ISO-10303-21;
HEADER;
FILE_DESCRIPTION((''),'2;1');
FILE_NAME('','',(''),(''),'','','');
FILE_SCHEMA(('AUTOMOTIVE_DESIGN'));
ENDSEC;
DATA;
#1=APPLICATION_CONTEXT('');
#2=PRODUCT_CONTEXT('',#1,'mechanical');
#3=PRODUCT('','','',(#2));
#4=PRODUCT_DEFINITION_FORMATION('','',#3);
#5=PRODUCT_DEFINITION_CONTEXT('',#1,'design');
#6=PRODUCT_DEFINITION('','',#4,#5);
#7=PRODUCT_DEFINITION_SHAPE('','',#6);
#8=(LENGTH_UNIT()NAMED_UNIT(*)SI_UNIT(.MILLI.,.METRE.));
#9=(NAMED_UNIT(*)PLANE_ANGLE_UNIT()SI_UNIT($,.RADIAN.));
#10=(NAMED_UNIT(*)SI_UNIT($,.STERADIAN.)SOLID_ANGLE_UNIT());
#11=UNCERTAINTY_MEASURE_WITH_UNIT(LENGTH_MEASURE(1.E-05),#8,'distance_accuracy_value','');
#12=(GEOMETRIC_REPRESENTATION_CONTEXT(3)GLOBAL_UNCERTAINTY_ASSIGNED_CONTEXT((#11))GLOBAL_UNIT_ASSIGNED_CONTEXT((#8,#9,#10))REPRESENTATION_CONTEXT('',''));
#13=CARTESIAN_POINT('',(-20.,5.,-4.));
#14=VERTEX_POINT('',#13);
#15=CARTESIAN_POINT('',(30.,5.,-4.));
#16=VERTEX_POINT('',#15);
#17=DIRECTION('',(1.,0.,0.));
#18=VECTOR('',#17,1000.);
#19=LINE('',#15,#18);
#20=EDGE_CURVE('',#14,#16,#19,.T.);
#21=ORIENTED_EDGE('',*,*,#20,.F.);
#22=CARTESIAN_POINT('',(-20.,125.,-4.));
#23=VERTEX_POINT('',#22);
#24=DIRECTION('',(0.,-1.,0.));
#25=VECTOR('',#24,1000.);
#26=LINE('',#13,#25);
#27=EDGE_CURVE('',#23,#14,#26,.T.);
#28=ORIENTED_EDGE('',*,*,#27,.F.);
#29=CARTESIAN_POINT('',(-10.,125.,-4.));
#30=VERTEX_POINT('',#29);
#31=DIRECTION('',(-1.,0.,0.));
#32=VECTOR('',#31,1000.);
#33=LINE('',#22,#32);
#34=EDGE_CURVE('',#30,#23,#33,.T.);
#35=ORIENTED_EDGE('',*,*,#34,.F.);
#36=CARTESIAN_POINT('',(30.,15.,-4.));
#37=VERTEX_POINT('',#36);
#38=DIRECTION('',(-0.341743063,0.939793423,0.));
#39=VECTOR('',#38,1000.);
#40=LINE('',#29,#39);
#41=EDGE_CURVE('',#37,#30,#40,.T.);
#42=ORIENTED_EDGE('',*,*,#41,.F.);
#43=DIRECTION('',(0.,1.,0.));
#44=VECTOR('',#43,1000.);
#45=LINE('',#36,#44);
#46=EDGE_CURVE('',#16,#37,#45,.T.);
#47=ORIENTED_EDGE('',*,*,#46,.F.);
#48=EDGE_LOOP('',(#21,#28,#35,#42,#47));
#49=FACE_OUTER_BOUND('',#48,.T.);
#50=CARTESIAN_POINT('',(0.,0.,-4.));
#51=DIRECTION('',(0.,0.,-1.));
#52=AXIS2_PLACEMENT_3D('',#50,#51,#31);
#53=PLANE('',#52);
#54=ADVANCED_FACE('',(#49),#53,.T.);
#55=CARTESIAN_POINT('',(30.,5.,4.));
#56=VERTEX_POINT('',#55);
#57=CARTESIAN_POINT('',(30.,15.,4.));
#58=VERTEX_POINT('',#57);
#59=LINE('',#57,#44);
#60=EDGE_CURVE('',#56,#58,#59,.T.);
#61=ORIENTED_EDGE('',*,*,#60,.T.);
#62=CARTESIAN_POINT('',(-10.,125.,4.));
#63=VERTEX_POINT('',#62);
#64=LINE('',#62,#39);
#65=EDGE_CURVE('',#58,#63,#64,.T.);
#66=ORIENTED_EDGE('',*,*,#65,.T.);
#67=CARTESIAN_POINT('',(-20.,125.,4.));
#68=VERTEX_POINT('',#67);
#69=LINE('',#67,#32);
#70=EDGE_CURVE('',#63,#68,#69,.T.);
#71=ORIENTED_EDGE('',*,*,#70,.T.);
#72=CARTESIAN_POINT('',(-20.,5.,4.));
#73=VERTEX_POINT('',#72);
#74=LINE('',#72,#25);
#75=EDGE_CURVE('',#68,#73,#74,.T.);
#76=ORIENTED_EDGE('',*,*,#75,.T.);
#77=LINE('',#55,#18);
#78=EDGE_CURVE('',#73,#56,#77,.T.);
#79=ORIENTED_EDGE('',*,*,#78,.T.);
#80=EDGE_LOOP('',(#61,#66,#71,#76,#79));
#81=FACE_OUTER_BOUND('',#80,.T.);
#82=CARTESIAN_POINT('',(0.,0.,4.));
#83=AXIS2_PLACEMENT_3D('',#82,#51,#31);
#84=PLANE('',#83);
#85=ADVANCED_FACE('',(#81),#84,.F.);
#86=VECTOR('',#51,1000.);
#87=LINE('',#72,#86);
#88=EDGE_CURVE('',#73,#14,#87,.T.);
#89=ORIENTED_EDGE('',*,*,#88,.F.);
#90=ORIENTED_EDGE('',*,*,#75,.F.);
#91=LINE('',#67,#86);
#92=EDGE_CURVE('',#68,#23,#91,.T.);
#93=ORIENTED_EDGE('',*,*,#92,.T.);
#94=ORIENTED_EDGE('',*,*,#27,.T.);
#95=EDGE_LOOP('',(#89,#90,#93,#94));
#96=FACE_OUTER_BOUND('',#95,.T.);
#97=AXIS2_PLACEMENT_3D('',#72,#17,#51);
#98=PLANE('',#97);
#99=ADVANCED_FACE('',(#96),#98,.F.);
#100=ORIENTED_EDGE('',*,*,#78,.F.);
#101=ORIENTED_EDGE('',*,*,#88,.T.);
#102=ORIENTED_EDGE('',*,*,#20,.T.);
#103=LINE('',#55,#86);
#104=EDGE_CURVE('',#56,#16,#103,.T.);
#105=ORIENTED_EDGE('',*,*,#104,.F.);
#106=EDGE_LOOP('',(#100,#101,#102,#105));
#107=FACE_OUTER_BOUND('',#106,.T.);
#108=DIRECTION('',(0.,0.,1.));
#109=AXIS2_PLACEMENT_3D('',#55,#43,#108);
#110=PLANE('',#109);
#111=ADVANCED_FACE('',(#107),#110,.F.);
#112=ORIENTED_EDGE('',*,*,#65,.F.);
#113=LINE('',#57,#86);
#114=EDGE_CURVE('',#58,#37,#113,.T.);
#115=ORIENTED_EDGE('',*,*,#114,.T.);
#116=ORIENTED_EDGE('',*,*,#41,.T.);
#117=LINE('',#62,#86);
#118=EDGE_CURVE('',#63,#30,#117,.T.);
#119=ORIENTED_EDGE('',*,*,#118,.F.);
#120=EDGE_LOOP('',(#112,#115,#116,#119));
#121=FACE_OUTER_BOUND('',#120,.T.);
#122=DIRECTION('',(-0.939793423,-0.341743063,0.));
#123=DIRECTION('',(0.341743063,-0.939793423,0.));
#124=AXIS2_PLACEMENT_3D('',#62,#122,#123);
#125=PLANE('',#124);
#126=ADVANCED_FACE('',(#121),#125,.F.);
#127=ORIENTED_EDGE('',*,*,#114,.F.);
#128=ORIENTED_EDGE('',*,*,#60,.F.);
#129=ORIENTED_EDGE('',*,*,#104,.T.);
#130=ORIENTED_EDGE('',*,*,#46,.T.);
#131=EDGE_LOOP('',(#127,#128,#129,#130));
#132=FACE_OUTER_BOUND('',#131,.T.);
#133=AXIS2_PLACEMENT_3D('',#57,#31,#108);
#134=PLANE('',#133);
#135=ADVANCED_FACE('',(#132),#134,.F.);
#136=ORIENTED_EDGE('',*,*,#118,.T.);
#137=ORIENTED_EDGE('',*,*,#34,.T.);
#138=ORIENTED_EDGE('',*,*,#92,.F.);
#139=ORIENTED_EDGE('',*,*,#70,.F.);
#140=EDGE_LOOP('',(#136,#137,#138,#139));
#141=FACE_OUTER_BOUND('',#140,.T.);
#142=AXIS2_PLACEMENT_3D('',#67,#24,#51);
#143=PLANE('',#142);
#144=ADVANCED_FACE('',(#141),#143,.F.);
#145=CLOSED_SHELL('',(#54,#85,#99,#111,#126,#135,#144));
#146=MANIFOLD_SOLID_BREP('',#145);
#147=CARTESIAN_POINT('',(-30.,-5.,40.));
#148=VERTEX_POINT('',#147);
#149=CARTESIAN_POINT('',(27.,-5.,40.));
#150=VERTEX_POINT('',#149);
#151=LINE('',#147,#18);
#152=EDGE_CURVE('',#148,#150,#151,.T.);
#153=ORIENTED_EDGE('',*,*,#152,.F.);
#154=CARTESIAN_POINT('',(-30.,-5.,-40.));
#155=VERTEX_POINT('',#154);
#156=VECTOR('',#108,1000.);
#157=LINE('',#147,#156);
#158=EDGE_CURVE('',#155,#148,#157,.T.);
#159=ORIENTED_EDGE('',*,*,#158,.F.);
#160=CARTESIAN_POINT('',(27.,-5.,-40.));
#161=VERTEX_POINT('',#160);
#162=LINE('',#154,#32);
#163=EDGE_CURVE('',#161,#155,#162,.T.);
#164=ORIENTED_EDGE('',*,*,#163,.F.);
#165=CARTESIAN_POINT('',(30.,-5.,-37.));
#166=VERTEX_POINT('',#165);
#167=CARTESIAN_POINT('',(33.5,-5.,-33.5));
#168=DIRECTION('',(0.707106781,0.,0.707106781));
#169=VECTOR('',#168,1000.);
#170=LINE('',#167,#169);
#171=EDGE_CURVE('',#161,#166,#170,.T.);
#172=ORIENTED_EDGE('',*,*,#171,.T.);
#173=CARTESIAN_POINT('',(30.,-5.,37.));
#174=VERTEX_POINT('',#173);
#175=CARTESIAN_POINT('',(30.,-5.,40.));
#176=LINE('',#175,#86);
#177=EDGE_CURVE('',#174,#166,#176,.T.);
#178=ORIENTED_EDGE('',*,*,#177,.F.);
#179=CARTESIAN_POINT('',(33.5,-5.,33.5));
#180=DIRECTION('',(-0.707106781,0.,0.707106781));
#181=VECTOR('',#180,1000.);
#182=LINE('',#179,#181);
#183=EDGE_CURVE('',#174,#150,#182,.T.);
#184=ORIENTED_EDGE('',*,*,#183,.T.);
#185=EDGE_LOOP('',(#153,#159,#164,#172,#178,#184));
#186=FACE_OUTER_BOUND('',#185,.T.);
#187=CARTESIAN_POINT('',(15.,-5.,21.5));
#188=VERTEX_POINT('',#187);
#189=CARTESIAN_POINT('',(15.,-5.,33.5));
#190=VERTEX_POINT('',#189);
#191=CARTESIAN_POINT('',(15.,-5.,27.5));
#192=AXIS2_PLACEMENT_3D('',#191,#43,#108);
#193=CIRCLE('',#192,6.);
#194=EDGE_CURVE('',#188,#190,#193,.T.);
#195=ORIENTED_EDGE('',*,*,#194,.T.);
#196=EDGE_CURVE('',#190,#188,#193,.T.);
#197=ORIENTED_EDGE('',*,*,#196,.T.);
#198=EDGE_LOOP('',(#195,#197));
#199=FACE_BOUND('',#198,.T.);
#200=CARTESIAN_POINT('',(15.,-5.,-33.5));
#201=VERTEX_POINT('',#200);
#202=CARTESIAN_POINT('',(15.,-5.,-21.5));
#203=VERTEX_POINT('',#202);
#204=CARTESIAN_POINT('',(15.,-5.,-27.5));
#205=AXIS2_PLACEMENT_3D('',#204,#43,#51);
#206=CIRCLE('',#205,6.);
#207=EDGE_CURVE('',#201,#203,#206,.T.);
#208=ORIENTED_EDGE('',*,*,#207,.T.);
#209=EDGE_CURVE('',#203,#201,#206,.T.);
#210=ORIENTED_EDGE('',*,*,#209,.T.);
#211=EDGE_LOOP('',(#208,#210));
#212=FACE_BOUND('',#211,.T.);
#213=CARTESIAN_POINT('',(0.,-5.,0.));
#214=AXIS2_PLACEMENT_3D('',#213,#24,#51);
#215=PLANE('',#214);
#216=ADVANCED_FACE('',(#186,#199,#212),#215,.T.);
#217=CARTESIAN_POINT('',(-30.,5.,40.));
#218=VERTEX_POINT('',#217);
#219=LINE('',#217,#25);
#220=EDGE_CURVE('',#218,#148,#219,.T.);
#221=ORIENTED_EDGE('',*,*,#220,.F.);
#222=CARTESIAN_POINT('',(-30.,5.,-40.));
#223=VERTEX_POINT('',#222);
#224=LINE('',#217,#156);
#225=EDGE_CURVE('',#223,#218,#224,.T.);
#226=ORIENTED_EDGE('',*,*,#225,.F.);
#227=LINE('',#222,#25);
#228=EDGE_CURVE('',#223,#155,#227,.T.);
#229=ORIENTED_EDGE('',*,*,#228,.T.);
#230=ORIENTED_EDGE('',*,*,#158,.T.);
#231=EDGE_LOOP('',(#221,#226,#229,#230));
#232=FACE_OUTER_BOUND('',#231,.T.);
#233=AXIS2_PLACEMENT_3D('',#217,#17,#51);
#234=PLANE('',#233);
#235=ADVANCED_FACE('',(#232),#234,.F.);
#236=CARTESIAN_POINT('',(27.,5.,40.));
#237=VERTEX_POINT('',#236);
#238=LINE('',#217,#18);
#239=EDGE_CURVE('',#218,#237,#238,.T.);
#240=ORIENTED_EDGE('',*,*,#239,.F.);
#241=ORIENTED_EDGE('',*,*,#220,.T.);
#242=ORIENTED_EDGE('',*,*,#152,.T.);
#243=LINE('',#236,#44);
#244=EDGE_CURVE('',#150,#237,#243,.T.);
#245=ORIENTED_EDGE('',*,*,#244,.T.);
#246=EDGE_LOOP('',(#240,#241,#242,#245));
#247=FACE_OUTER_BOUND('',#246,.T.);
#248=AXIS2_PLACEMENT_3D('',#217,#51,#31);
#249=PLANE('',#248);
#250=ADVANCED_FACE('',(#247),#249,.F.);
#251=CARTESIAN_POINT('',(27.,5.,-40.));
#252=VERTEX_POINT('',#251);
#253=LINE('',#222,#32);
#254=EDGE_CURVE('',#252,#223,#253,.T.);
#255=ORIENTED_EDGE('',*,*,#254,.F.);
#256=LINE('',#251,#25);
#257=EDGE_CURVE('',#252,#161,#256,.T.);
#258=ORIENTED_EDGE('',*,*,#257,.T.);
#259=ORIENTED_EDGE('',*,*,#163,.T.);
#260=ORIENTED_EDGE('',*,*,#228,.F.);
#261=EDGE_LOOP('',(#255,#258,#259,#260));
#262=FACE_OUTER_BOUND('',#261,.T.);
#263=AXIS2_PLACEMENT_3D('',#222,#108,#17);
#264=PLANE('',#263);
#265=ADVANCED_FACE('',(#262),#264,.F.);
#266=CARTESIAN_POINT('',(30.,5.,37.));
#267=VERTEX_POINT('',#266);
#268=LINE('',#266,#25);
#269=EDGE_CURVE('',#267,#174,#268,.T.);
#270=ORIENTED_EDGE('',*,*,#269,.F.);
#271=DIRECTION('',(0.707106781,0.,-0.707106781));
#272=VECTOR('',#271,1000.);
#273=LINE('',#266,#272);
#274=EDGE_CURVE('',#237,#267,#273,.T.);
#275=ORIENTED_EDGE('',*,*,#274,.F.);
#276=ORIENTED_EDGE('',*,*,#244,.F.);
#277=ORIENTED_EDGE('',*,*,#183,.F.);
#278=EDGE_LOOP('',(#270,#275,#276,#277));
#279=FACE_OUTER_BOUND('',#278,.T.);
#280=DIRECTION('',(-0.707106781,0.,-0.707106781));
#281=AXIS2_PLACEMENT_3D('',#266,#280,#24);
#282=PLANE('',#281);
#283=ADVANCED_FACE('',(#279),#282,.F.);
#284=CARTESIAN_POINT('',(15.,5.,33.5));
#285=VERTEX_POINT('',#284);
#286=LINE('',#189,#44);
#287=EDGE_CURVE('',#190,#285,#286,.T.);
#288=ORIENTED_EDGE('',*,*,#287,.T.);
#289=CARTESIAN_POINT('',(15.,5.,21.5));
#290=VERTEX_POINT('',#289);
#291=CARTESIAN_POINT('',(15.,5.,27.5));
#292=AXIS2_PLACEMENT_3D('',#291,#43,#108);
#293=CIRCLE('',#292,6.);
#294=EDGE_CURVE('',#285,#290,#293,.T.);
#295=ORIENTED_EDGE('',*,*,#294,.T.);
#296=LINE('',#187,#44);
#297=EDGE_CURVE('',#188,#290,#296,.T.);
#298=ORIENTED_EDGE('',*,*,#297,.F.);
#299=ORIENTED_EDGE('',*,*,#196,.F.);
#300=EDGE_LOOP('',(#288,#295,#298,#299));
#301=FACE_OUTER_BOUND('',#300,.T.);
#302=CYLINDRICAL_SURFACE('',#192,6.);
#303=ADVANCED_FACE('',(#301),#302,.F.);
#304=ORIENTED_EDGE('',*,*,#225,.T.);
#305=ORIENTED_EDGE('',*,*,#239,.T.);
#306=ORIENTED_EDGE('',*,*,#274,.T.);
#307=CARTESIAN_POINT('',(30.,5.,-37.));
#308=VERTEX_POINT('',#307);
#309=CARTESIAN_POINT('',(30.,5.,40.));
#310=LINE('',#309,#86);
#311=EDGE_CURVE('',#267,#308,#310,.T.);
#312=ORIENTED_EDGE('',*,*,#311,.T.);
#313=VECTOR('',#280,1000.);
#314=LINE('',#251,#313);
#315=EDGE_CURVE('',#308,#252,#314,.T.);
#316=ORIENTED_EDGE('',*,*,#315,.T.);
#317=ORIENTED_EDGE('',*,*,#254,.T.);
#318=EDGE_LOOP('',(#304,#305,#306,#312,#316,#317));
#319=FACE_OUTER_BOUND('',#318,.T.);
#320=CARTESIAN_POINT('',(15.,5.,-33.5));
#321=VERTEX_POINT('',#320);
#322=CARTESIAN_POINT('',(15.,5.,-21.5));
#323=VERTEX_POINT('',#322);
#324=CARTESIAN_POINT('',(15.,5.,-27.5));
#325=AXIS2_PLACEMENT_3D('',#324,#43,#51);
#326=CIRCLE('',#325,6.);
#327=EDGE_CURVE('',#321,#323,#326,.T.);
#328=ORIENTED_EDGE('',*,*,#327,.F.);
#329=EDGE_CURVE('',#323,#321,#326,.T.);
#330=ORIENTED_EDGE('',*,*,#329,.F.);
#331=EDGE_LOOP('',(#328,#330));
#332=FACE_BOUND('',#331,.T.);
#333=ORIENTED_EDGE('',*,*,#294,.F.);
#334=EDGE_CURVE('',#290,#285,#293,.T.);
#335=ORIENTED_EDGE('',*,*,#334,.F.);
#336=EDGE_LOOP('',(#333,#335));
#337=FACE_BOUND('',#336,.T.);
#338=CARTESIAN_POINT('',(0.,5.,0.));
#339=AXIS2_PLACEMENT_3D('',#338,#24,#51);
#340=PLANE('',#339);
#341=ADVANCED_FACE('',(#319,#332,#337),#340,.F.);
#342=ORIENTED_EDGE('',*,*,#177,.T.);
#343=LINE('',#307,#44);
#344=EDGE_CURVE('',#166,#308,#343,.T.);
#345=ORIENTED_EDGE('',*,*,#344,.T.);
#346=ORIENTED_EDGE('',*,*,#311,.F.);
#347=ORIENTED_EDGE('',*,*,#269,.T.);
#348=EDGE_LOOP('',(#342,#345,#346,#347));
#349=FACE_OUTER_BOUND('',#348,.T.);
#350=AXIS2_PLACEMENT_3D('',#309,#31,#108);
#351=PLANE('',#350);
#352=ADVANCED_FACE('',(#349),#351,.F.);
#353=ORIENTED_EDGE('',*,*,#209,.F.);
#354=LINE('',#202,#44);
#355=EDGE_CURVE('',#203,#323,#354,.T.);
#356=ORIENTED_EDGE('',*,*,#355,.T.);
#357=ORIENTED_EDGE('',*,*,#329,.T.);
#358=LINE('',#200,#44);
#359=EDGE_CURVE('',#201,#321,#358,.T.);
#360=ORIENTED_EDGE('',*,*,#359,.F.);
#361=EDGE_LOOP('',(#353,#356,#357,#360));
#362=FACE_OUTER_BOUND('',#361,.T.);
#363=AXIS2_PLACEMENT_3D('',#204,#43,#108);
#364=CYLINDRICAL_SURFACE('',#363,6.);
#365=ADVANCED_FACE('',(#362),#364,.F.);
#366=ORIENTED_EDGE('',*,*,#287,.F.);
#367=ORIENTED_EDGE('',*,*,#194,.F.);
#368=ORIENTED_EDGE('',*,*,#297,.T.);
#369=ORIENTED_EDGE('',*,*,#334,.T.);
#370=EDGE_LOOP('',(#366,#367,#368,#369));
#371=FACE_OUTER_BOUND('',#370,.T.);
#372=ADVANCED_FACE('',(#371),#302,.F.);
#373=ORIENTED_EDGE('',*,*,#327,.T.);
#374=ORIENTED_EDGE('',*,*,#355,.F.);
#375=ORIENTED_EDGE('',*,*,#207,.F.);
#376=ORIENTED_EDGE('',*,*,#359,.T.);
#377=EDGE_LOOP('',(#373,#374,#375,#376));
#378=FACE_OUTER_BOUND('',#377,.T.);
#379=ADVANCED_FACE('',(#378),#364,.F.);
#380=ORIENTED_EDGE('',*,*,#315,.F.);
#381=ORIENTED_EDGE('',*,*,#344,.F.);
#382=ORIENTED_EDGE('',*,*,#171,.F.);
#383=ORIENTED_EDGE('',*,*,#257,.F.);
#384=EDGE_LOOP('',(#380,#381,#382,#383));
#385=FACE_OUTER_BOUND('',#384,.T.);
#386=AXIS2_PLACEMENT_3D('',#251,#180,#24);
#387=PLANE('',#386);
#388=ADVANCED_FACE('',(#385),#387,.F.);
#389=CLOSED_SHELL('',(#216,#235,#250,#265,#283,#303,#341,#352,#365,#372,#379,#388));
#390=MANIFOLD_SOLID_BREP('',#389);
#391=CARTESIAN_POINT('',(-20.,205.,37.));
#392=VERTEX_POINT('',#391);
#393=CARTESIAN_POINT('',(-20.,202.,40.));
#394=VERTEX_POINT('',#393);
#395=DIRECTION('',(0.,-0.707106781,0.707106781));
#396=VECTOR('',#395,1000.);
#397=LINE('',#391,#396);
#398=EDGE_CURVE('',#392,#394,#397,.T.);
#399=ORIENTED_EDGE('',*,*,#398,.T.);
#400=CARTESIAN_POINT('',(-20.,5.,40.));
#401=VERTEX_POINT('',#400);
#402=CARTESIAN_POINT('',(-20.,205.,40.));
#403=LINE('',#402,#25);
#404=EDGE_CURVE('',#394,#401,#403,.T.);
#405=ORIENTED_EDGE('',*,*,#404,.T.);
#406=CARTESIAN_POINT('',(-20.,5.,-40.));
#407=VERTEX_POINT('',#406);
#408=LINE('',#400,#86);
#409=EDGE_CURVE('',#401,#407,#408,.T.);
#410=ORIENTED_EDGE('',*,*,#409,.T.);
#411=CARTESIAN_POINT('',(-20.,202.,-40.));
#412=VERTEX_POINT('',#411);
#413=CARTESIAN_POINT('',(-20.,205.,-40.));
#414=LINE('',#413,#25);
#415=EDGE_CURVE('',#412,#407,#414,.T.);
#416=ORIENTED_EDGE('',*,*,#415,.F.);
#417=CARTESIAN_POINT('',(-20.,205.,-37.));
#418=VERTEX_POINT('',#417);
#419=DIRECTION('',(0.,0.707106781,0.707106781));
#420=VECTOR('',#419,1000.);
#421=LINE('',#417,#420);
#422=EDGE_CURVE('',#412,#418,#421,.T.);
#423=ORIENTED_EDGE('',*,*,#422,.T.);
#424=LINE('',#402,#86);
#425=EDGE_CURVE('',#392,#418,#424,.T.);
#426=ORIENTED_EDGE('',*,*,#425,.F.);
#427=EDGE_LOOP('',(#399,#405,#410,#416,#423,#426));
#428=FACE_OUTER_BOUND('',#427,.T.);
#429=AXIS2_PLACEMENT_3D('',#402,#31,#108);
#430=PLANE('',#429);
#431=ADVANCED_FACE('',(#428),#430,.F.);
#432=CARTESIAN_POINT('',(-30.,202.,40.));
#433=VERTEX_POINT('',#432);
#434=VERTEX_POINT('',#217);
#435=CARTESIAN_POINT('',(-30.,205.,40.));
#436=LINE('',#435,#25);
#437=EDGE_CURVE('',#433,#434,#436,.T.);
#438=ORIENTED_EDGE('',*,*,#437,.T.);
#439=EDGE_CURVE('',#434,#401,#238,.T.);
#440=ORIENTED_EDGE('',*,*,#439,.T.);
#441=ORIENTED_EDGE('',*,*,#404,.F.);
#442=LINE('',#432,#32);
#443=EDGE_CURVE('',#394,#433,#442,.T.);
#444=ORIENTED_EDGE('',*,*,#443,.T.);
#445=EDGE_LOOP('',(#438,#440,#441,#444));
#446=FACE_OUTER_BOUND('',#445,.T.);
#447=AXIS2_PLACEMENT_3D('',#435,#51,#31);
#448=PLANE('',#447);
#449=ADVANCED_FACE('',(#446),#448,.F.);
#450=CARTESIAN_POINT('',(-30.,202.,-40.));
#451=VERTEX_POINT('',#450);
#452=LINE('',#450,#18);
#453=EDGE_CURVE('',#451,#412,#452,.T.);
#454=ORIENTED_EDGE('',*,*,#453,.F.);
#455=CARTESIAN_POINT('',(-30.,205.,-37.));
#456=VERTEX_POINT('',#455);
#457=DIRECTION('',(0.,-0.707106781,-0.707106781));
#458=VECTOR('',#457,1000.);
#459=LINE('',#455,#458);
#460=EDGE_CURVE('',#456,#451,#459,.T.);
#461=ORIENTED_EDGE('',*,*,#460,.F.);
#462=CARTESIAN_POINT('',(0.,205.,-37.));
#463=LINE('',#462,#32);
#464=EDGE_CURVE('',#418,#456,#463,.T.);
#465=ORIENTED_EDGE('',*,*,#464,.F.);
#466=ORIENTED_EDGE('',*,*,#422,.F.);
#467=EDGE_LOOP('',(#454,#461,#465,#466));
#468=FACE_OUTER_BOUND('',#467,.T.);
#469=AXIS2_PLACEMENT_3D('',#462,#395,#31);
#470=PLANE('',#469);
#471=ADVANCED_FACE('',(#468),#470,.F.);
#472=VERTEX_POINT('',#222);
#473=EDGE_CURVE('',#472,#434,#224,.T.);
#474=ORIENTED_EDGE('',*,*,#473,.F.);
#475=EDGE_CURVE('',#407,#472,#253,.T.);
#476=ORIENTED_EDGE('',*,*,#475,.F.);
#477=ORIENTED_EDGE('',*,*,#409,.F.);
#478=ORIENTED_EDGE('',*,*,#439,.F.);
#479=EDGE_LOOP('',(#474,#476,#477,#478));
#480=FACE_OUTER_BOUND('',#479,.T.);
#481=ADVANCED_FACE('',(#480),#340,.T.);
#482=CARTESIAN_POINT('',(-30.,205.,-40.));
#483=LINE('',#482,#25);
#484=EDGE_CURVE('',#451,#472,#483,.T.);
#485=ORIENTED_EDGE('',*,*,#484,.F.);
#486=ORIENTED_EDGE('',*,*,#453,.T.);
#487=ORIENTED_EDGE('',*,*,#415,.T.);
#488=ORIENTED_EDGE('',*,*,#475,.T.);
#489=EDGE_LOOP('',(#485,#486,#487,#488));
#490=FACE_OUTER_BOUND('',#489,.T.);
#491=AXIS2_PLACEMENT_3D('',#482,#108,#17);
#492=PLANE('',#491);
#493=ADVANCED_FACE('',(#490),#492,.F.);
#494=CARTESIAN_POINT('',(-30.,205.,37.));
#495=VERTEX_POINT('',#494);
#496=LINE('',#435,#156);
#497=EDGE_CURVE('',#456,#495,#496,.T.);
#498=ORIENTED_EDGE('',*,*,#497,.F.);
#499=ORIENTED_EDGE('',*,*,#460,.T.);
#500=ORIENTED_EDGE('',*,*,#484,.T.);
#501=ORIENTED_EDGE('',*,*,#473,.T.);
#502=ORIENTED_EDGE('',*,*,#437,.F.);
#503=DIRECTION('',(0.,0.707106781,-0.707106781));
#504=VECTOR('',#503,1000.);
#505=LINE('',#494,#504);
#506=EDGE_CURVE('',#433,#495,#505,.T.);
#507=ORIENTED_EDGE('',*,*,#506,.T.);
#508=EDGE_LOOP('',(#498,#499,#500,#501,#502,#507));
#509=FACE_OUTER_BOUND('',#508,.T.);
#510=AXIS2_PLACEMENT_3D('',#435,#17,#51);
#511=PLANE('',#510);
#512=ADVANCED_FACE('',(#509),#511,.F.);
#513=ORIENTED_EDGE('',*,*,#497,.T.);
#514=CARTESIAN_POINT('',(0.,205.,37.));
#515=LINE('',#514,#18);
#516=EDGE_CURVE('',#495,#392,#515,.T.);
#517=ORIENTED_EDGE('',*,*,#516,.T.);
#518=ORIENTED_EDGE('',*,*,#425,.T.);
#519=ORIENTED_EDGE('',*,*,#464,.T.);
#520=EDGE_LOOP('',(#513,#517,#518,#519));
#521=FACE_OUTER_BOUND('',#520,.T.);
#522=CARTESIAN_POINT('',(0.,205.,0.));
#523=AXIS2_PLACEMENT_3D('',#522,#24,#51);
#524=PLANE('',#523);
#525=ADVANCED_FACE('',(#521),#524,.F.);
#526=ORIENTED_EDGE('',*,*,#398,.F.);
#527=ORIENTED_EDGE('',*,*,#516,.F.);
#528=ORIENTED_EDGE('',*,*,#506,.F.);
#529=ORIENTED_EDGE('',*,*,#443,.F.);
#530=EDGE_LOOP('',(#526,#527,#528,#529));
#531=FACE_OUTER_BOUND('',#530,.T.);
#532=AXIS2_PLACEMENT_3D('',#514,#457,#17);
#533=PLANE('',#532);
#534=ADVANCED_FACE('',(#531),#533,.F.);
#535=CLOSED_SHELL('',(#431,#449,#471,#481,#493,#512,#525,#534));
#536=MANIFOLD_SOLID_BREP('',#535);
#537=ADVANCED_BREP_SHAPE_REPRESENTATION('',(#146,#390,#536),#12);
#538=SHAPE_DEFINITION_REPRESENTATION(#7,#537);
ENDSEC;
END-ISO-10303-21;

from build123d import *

# Parameters (mm, degrees)
SKETCH_1_W          = 60
SKETCH_1_H          = 80
EXTRUDE_1_DEPTH     = 5
SKETCH_2_W          = 10
SKETCH_2_H          = 80
EXTRUDE_2_DEPTH     = 200
CHAMFER_1_SIZE      = 3
CHAMFER_2_SIZE      = 3
EXTRUDE_3_DEPTH     = 4
SKETCH_7_R          = 6
CUT_EXTRUDE_1_DEPTH = 10


with BuildPart() as part:
    # 草图1 → 凸台-拉伸1 (new, symmetric)
    with BuildSketch(Plane(origin=(0, 0, 0), x_dir=(1, 0, 0), z_dir=(0, 1, 0))):
        Rectangle(SKETCH_1_W, SKETCH_1_H)
    extrude(amount=EXTRUDE_1_DEPTH, both=True)

    # 倒角1
    chamfer_1_edges = [part.edges().sort_by_distance(p)[0] for p in [
        (30, 0, 40),
        (30, 0, -40),
    ]]
    chamfer(chamfer_1_edges, length=CHAMFER_1_SIZE)

    # 草图7 → 切除-拉伸1 (cut)
    with BuildSketch(Plane(origin=(0, 5, 0), x_dir=(1, 0, 0), z_dir=(0, 1, 0))):
        with Locations(Location((15, -27.5, 0), (0, 0, 270))):
            Circle(SKETCH_7_R)
        with Locations(Location((15, 27.5, 0), (0, 0, 90))):
            Circle(SKETCH_7_R)
    extrude(amount=-CUT_EXTRUDE_1_DEPTH, mode=Mode.SUBTRACT)


with BuildPart() as body_2:
    # 草图2 → 凸台-拉伸2 (new body)
    with BuildSketch(Plane(origin=(0, 5, 0), x_dir=(1, 0, 0), z_dir=(0, 1, 0))):
        with Locations((-25, 0)):
            Rectangle(SKETCH_2_W, SKETCH_2_H)
    extrude(amount=EXTRUDE_2_DEPTH)

    # 倒角2
    chamfer_2_edges = [body_2.edges().sort_by_distance(p)[0] for p in [
        (-25, 205, -40),
        (-25, 205, 40),
    ]]
    chamfer(chamfer_2_edges, length=CHAMFER_2_SIZE)


with BuildPart() as body_3:
    # 草图6 → 凸台-拉伸3 (new, symmetric)
    with BuildSketch(Plane.XY):
        Polygon((-20, 125), (-10, 125), (30, 15), (30, 5), (-20, 5), align=None)
    extrude(amount=EXTRUDE_3_DEPTH, both=True)


solid = Compound([part.part, body_2.part, body_3.part])
